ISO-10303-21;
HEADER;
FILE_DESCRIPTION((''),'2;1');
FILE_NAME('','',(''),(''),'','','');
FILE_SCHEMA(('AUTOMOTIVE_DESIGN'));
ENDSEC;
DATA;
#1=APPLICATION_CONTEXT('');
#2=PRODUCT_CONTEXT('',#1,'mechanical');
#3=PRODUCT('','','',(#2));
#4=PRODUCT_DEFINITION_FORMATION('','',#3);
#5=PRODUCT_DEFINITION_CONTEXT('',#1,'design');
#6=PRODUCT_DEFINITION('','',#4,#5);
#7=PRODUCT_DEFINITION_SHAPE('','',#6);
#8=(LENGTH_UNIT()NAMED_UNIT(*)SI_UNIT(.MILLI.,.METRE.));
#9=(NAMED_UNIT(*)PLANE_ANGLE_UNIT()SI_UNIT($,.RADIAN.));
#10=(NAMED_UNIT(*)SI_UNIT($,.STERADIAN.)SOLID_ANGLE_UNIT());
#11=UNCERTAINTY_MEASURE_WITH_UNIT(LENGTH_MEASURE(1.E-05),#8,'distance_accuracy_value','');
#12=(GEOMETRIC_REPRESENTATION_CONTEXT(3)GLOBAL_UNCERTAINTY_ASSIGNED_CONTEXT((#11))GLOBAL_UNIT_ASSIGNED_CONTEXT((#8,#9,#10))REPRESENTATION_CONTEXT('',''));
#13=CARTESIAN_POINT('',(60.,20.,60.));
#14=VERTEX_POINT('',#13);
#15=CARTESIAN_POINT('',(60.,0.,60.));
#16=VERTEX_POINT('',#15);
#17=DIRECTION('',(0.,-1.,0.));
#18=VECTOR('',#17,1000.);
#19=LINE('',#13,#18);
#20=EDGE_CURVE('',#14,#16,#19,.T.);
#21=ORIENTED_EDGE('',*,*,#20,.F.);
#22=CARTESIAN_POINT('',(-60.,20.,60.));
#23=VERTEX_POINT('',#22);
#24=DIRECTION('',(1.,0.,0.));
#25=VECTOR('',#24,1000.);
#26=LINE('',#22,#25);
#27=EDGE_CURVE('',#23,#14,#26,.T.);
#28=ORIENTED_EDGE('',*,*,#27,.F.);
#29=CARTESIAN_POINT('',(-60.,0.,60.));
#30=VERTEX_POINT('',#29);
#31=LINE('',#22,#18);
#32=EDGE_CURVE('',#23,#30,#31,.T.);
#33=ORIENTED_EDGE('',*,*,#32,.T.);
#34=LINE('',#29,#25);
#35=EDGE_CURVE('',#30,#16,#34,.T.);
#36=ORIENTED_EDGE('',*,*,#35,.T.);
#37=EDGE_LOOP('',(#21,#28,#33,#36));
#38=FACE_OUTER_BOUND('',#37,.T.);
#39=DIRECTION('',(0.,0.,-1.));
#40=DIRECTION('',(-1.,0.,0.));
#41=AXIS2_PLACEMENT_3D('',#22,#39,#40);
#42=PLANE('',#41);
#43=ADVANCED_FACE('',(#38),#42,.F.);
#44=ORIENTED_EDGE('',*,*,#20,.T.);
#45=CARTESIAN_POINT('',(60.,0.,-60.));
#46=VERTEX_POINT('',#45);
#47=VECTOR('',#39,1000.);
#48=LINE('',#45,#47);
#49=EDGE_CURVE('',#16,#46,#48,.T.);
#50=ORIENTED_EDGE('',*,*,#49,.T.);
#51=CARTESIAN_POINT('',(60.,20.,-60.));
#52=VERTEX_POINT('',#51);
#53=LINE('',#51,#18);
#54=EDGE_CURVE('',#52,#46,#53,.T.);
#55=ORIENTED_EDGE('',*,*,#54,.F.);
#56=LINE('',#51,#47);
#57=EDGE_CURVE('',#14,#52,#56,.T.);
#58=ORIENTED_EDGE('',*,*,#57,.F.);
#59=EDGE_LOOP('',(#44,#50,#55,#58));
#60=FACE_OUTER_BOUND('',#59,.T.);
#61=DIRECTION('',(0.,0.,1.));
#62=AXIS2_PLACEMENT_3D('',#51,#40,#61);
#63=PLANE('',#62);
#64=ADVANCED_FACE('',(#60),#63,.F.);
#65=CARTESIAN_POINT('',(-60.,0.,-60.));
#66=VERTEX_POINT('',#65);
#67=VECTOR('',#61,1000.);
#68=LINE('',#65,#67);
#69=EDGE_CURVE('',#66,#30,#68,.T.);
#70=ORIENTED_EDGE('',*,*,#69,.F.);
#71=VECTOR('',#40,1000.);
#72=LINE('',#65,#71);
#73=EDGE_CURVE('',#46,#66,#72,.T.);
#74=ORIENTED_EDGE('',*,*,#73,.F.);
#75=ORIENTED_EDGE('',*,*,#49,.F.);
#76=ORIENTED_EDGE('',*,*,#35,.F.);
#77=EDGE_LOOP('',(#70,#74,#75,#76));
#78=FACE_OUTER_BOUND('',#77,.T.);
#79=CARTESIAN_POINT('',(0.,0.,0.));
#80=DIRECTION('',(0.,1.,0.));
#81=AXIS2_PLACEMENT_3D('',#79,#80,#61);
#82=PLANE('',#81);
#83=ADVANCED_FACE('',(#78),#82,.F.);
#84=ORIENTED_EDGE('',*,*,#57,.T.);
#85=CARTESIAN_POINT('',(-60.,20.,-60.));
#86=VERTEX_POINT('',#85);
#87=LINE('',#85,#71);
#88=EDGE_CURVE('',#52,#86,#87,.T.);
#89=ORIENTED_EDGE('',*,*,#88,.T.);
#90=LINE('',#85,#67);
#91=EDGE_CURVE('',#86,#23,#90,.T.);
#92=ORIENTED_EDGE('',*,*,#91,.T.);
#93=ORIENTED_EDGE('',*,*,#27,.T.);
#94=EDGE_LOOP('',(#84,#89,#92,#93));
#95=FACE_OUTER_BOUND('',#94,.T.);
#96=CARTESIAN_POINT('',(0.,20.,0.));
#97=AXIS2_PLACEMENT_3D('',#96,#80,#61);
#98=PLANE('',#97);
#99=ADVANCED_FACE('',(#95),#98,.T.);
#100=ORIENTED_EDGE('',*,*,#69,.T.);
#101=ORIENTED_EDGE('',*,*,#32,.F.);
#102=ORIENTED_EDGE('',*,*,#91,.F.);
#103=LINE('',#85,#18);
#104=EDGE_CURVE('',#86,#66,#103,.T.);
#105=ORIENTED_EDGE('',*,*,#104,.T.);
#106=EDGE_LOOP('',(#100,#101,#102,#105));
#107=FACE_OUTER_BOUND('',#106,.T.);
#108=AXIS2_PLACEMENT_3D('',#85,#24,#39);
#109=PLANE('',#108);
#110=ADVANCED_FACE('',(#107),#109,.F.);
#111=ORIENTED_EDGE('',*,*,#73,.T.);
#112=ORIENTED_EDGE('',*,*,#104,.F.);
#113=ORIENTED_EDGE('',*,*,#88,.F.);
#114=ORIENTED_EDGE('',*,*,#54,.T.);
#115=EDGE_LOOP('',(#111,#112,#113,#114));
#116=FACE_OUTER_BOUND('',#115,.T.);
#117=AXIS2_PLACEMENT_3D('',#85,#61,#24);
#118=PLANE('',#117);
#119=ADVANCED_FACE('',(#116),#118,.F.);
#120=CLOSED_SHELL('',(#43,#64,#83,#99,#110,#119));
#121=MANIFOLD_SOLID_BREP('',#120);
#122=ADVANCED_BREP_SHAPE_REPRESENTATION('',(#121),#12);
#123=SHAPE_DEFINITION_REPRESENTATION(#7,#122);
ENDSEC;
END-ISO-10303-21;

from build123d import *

# Parameters (mm, degrees)
SKETCH1_W           = 120
SKETCH1_H           = 120
BOSS_EXTRUDE1_DEPTH = 20


with BuildPart() as part:
    # Sketch1 → Boss-Extrude1 (new body)
    with BuildSketch(Plane(origin=(0, 0, 0), x_dir=(1, 0, 0), z_dir=(0, 1, 0))):
        Rectangle(SKETCH1_W, SKETCH1_H)
    extrude(amount=BOSS_EXTRUDE1_DEPTH)


solid = part.part
